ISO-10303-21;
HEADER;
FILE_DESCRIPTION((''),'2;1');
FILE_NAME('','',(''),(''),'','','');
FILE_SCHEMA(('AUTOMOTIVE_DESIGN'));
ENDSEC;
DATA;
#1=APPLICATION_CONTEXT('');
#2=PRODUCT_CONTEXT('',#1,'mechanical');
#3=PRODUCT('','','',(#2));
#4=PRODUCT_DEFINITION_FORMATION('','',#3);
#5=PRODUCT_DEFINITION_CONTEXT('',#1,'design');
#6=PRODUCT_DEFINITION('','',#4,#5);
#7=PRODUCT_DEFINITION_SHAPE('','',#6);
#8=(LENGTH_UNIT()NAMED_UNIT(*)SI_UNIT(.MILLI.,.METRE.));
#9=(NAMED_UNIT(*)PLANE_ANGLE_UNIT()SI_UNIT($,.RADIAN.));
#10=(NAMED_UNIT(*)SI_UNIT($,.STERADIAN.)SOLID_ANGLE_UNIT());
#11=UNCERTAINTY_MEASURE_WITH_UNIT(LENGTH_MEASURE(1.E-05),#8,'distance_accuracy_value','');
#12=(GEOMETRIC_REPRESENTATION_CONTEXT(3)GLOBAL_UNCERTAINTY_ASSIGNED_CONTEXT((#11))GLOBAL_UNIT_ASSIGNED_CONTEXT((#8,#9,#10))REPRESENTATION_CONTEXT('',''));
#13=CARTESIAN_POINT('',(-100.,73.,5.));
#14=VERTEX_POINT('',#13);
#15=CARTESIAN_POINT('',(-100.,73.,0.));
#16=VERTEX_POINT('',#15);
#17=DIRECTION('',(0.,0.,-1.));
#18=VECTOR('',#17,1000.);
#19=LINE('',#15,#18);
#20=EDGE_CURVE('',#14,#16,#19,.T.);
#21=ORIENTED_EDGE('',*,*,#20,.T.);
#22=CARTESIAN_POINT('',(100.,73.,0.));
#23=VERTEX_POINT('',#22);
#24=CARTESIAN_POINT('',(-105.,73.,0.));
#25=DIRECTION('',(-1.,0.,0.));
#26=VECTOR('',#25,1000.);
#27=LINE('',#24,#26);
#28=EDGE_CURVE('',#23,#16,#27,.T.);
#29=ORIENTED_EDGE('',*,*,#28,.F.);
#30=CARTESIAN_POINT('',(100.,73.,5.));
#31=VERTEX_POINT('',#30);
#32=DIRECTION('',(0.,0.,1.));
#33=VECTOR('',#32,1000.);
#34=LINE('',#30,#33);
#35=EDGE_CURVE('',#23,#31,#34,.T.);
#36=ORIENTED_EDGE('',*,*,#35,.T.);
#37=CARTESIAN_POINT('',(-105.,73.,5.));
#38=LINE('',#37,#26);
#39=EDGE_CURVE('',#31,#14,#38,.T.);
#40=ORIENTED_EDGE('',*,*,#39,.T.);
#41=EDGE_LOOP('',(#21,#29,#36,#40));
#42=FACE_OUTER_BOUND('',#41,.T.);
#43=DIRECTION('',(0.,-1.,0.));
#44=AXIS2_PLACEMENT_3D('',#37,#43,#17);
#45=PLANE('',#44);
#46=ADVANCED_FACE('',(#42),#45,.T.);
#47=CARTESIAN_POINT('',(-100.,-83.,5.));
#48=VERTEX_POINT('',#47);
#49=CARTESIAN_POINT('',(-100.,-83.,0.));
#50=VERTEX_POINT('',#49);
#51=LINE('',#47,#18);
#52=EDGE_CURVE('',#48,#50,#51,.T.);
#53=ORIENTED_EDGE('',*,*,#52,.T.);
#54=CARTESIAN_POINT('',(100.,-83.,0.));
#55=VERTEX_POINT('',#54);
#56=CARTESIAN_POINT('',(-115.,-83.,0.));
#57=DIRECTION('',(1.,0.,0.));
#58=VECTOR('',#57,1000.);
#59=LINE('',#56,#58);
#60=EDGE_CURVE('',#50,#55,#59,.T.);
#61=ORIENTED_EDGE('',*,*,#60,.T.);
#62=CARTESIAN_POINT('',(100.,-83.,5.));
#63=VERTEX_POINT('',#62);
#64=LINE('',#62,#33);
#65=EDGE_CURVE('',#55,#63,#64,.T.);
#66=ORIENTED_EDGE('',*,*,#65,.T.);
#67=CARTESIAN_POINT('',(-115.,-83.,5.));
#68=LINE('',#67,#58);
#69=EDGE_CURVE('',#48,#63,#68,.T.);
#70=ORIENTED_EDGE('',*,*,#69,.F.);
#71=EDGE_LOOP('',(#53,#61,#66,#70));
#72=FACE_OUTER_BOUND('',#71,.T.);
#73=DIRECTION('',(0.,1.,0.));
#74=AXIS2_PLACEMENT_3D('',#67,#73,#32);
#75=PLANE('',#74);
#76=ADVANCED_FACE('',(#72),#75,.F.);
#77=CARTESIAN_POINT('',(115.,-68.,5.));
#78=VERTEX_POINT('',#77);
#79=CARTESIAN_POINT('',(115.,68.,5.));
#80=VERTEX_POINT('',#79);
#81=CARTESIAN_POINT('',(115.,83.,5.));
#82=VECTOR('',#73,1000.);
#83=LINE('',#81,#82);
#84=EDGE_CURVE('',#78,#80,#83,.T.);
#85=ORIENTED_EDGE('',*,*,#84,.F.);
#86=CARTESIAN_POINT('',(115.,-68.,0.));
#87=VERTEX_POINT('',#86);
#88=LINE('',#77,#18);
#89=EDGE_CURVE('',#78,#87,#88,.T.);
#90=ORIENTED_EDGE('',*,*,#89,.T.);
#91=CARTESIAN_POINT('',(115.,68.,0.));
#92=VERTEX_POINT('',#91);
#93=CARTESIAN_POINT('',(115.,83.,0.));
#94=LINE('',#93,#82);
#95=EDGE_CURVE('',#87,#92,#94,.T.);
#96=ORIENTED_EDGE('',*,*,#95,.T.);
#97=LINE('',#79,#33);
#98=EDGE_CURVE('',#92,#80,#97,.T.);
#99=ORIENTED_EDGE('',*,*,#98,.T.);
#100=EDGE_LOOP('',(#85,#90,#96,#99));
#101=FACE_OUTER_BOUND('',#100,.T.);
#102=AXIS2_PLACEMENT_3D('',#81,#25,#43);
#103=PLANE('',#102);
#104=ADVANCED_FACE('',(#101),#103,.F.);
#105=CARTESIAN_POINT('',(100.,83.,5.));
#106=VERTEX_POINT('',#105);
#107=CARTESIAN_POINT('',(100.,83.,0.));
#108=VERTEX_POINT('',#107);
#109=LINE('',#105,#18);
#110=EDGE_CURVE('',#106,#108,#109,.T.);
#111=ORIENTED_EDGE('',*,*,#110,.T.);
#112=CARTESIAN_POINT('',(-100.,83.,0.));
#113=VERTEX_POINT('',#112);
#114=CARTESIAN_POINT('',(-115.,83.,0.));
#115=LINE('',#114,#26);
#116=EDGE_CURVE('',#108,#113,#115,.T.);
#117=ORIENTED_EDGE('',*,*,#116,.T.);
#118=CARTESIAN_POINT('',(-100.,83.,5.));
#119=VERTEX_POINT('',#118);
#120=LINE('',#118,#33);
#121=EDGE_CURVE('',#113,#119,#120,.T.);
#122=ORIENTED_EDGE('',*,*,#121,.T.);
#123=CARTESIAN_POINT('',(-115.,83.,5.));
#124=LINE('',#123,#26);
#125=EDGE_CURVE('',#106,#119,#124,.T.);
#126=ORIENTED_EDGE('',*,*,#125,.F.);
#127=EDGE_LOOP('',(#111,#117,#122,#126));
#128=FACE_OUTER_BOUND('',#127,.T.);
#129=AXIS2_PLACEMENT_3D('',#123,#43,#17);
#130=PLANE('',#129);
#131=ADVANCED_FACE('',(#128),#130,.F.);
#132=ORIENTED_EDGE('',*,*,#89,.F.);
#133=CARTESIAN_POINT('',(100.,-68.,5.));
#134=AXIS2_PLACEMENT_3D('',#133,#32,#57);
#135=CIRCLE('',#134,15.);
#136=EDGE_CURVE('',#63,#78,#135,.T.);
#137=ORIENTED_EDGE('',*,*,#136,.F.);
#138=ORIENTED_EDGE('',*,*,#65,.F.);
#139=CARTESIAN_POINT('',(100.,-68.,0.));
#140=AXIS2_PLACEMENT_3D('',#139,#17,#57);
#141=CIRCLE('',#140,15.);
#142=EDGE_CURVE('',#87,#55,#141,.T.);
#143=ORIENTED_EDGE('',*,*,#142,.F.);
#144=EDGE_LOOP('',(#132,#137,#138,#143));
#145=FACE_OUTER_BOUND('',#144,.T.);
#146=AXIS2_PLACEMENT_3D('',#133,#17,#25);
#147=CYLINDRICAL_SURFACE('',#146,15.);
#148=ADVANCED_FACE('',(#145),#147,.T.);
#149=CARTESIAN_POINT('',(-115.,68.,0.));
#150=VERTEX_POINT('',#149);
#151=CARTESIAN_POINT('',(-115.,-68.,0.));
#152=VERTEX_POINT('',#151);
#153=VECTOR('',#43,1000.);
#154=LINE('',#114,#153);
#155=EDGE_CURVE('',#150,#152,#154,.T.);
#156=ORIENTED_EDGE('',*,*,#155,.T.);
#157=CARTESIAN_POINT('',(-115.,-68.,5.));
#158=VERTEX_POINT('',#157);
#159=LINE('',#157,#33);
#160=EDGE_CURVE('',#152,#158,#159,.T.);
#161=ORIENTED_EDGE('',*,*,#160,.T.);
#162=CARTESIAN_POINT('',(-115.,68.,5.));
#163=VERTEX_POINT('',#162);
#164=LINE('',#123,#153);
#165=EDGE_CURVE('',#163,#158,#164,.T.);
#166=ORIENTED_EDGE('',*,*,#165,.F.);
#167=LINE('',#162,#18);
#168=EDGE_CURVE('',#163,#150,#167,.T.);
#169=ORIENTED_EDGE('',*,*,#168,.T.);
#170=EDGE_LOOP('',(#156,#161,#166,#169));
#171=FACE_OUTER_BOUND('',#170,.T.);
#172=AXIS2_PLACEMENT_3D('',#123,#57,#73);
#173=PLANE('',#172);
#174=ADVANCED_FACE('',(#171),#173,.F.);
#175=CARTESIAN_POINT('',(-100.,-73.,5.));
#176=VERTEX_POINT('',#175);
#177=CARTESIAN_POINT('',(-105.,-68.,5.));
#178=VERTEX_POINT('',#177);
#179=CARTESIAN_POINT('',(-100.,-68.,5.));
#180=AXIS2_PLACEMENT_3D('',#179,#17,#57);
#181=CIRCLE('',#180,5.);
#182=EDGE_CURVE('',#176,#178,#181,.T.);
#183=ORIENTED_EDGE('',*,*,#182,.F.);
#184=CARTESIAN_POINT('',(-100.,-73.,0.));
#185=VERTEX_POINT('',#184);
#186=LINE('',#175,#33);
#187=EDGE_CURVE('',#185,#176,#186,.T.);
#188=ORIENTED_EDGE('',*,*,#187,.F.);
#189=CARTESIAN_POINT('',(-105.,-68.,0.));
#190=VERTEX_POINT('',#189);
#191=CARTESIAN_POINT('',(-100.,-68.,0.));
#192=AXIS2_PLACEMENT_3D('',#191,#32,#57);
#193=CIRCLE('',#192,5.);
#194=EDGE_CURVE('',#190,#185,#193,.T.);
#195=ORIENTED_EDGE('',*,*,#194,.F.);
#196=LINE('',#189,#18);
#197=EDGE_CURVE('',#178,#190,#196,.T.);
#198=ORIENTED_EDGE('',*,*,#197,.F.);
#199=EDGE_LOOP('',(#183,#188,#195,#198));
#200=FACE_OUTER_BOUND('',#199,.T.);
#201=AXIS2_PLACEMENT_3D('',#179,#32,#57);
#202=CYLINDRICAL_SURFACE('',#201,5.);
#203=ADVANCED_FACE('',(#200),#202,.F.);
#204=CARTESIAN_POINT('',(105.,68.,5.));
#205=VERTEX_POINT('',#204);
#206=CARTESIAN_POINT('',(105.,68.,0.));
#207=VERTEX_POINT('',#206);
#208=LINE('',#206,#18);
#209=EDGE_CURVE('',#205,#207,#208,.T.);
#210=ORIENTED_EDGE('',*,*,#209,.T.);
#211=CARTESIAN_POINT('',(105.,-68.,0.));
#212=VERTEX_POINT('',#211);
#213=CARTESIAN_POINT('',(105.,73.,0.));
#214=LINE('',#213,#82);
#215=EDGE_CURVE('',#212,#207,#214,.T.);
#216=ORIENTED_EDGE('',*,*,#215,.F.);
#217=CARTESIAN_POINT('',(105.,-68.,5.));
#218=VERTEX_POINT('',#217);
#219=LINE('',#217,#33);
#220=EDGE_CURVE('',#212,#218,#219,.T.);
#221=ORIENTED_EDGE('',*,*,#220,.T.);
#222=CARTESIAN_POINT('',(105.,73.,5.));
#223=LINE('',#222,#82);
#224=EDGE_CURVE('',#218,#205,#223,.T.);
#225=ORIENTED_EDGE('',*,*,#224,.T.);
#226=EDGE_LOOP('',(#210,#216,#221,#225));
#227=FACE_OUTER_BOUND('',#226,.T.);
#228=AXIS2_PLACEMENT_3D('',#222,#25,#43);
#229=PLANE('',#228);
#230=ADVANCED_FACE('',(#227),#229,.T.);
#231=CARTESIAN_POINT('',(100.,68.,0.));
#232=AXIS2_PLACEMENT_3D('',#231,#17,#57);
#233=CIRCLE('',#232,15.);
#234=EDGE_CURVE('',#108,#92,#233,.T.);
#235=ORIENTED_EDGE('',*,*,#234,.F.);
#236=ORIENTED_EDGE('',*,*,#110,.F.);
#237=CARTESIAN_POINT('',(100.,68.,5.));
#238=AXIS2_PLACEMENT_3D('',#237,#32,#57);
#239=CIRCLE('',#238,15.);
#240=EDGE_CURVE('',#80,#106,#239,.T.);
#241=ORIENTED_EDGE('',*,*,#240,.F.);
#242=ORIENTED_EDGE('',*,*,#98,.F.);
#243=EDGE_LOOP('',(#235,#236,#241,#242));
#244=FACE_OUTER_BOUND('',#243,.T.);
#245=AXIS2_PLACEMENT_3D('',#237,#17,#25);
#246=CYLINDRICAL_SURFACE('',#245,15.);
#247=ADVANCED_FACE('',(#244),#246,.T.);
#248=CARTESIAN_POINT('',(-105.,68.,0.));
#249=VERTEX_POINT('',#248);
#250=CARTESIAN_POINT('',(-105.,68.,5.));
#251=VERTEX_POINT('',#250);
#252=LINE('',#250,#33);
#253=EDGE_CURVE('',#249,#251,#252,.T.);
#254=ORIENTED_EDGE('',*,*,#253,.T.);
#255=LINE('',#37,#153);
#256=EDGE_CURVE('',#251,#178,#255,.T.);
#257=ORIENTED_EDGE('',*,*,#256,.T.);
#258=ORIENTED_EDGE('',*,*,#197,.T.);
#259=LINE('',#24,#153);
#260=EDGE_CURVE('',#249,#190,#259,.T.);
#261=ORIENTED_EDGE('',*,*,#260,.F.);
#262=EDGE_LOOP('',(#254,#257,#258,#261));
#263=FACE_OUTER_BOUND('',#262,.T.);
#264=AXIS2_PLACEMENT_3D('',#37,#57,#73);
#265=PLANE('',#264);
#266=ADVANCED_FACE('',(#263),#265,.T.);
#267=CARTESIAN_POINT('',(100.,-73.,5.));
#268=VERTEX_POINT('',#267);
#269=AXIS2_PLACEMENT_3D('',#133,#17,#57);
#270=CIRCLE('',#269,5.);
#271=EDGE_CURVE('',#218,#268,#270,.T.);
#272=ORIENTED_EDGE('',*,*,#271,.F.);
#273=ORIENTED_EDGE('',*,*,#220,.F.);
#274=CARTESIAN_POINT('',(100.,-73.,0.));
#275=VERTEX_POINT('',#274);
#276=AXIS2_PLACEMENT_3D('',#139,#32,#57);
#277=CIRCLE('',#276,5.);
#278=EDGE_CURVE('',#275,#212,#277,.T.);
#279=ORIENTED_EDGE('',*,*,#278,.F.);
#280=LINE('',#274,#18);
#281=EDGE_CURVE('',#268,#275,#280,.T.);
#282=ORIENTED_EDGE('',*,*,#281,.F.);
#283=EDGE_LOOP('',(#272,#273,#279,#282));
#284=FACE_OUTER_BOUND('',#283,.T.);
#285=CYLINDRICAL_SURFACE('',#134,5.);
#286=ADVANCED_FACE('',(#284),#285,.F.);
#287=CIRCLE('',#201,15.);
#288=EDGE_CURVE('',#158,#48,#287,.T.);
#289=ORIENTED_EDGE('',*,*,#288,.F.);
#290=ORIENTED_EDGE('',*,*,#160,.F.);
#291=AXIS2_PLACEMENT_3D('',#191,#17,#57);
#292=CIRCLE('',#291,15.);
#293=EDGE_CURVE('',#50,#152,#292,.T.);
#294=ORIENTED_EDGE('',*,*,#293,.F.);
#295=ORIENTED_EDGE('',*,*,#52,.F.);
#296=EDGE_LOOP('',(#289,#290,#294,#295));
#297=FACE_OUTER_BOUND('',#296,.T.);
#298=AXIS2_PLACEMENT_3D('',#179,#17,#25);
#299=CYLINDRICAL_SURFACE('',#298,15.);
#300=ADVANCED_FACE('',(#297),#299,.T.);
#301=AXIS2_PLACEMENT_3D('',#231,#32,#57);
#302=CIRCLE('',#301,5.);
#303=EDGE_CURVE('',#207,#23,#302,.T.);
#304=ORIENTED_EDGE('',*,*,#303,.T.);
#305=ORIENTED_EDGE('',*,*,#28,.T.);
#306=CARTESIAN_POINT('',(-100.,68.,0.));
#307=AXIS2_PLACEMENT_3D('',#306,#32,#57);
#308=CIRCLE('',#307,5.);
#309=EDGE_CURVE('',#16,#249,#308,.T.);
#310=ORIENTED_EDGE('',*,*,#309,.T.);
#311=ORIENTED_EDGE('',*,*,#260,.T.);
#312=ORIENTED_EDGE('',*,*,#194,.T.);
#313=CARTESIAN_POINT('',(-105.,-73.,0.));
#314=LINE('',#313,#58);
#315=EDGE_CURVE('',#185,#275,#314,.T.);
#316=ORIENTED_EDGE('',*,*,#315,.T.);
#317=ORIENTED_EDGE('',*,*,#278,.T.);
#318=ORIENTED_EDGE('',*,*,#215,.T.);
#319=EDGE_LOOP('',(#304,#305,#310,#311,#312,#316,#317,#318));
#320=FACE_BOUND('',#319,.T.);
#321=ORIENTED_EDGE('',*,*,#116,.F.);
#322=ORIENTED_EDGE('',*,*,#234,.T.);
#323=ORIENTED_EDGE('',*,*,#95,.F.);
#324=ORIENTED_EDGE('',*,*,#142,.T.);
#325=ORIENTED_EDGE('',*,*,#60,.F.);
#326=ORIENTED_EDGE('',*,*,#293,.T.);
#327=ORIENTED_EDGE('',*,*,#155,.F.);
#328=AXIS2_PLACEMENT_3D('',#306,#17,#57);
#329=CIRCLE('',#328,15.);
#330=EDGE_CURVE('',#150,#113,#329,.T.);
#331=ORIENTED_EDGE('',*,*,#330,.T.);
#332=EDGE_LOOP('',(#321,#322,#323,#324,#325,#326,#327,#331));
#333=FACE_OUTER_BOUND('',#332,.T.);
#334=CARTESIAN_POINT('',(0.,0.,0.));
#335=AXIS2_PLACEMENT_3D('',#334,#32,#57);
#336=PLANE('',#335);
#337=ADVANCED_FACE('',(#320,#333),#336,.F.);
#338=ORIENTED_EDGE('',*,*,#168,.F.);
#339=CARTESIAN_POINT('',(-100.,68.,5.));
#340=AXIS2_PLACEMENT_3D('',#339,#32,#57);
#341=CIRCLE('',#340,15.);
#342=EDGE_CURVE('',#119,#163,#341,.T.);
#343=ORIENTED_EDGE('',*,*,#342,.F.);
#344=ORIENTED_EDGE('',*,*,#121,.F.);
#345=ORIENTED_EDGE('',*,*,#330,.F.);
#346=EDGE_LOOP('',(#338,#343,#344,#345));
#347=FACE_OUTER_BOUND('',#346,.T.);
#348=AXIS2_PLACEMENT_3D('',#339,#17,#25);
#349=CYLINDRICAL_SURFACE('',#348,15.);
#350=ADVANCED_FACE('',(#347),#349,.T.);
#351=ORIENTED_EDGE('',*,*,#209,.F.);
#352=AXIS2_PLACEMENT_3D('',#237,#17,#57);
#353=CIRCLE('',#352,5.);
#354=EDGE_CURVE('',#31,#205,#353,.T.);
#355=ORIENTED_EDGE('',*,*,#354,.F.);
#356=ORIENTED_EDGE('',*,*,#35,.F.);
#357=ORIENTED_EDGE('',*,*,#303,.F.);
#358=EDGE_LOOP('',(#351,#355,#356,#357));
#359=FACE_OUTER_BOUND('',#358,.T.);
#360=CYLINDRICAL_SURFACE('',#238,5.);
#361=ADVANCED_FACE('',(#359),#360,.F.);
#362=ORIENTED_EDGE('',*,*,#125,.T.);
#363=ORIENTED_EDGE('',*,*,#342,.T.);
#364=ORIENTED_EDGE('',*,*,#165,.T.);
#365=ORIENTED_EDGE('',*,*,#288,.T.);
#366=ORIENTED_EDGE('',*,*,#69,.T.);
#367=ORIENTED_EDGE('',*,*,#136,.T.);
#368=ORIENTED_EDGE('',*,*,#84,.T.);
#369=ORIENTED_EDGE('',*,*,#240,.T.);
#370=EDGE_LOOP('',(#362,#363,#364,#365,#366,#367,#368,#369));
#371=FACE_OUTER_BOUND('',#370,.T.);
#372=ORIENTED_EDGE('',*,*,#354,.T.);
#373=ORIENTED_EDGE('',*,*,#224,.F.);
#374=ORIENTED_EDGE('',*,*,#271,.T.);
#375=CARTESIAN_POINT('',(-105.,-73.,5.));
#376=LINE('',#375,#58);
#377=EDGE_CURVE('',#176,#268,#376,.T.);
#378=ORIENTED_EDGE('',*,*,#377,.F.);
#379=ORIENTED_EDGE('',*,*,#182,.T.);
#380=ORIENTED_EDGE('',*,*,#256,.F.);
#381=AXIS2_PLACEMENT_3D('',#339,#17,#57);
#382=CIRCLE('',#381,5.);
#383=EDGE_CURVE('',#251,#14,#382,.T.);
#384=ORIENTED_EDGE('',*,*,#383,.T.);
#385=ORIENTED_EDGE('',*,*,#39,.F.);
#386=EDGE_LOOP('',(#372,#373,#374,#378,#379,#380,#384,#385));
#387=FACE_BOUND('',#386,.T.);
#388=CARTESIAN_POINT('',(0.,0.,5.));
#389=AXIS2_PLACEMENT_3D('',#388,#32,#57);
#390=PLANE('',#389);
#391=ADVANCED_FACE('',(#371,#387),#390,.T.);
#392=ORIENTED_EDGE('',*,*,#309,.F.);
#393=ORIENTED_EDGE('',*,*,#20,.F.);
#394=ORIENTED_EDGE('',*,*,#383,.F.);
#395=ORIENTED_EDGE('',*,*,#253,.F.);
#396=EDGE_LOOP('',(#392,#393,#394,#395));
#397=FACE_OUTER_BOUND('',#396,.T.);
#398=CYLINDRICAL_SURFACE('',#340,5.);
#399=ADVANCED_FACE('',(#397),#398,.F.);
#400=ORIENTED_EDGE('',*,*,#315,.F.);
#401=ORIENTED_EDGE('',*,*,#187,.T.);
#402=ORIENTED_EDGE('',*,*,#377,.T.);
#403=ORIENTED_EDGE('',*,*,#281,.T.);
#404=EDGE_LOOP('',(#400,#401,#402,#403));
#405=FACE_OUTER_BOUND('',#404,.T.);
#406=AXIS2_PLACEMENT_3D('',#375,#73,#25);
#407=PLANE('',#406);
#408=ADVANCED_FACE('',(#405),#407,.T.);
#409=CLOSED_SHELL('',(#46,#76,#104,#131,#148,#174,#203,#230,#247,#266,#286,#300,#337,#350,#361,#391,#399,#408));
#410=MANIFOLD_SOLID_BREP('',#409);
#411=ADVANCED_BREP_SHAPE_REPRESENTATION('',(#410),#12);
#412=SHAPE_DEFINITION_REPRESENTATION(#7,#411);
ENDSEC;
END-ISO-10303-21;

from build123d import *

# Parameters (mm, degrees)
SKETCH1_W           = 230
SKETCH1_H           = 166
SKETCH1_W_2         = 210
SKETCH1_H_2         = 146
BOSS_EXTRUDE1_DEPTH = 5
FILLET1_R           = 5
FILLET2_R           = 15


with BuildPart() as part:
    # Sketch1 → Boss-Extrude1 (new body)
    with BuildSketch(Plane.XY):
        Rectangle(SKETCH1_W, SKETCH1_H)
        Rectangle(SKETCH1_W_2, SKETCH1_H_2, mode=Mode.SUBTRACT)
    extrude(amount=BOSS_EXTRUDE1_DEPTH)

    # Fillet1
    fillet1_edges = [part.edges().sort_by_distance(p)[0] for p in [
        (-105, 73, 2.5),
        (-105, -73, 2.5),
        (105, -73, 2.5),
        (105, 73, 2.5),
    ]]
    fillet(fillet1_edges, radius=FILLET1_R)

    # Fillet2
    fillet2_edges = [part.edges().sort_by_distance(p)[0] for p in [
        (-115, 83, 2.5),
        (115, 83, 2.5),
        (115, -83, 2.5),
        (-115, -83, 2.5),
    ]]
    fillet(fillet2_edges, radius=FILLET2_R)


solid = part.part
